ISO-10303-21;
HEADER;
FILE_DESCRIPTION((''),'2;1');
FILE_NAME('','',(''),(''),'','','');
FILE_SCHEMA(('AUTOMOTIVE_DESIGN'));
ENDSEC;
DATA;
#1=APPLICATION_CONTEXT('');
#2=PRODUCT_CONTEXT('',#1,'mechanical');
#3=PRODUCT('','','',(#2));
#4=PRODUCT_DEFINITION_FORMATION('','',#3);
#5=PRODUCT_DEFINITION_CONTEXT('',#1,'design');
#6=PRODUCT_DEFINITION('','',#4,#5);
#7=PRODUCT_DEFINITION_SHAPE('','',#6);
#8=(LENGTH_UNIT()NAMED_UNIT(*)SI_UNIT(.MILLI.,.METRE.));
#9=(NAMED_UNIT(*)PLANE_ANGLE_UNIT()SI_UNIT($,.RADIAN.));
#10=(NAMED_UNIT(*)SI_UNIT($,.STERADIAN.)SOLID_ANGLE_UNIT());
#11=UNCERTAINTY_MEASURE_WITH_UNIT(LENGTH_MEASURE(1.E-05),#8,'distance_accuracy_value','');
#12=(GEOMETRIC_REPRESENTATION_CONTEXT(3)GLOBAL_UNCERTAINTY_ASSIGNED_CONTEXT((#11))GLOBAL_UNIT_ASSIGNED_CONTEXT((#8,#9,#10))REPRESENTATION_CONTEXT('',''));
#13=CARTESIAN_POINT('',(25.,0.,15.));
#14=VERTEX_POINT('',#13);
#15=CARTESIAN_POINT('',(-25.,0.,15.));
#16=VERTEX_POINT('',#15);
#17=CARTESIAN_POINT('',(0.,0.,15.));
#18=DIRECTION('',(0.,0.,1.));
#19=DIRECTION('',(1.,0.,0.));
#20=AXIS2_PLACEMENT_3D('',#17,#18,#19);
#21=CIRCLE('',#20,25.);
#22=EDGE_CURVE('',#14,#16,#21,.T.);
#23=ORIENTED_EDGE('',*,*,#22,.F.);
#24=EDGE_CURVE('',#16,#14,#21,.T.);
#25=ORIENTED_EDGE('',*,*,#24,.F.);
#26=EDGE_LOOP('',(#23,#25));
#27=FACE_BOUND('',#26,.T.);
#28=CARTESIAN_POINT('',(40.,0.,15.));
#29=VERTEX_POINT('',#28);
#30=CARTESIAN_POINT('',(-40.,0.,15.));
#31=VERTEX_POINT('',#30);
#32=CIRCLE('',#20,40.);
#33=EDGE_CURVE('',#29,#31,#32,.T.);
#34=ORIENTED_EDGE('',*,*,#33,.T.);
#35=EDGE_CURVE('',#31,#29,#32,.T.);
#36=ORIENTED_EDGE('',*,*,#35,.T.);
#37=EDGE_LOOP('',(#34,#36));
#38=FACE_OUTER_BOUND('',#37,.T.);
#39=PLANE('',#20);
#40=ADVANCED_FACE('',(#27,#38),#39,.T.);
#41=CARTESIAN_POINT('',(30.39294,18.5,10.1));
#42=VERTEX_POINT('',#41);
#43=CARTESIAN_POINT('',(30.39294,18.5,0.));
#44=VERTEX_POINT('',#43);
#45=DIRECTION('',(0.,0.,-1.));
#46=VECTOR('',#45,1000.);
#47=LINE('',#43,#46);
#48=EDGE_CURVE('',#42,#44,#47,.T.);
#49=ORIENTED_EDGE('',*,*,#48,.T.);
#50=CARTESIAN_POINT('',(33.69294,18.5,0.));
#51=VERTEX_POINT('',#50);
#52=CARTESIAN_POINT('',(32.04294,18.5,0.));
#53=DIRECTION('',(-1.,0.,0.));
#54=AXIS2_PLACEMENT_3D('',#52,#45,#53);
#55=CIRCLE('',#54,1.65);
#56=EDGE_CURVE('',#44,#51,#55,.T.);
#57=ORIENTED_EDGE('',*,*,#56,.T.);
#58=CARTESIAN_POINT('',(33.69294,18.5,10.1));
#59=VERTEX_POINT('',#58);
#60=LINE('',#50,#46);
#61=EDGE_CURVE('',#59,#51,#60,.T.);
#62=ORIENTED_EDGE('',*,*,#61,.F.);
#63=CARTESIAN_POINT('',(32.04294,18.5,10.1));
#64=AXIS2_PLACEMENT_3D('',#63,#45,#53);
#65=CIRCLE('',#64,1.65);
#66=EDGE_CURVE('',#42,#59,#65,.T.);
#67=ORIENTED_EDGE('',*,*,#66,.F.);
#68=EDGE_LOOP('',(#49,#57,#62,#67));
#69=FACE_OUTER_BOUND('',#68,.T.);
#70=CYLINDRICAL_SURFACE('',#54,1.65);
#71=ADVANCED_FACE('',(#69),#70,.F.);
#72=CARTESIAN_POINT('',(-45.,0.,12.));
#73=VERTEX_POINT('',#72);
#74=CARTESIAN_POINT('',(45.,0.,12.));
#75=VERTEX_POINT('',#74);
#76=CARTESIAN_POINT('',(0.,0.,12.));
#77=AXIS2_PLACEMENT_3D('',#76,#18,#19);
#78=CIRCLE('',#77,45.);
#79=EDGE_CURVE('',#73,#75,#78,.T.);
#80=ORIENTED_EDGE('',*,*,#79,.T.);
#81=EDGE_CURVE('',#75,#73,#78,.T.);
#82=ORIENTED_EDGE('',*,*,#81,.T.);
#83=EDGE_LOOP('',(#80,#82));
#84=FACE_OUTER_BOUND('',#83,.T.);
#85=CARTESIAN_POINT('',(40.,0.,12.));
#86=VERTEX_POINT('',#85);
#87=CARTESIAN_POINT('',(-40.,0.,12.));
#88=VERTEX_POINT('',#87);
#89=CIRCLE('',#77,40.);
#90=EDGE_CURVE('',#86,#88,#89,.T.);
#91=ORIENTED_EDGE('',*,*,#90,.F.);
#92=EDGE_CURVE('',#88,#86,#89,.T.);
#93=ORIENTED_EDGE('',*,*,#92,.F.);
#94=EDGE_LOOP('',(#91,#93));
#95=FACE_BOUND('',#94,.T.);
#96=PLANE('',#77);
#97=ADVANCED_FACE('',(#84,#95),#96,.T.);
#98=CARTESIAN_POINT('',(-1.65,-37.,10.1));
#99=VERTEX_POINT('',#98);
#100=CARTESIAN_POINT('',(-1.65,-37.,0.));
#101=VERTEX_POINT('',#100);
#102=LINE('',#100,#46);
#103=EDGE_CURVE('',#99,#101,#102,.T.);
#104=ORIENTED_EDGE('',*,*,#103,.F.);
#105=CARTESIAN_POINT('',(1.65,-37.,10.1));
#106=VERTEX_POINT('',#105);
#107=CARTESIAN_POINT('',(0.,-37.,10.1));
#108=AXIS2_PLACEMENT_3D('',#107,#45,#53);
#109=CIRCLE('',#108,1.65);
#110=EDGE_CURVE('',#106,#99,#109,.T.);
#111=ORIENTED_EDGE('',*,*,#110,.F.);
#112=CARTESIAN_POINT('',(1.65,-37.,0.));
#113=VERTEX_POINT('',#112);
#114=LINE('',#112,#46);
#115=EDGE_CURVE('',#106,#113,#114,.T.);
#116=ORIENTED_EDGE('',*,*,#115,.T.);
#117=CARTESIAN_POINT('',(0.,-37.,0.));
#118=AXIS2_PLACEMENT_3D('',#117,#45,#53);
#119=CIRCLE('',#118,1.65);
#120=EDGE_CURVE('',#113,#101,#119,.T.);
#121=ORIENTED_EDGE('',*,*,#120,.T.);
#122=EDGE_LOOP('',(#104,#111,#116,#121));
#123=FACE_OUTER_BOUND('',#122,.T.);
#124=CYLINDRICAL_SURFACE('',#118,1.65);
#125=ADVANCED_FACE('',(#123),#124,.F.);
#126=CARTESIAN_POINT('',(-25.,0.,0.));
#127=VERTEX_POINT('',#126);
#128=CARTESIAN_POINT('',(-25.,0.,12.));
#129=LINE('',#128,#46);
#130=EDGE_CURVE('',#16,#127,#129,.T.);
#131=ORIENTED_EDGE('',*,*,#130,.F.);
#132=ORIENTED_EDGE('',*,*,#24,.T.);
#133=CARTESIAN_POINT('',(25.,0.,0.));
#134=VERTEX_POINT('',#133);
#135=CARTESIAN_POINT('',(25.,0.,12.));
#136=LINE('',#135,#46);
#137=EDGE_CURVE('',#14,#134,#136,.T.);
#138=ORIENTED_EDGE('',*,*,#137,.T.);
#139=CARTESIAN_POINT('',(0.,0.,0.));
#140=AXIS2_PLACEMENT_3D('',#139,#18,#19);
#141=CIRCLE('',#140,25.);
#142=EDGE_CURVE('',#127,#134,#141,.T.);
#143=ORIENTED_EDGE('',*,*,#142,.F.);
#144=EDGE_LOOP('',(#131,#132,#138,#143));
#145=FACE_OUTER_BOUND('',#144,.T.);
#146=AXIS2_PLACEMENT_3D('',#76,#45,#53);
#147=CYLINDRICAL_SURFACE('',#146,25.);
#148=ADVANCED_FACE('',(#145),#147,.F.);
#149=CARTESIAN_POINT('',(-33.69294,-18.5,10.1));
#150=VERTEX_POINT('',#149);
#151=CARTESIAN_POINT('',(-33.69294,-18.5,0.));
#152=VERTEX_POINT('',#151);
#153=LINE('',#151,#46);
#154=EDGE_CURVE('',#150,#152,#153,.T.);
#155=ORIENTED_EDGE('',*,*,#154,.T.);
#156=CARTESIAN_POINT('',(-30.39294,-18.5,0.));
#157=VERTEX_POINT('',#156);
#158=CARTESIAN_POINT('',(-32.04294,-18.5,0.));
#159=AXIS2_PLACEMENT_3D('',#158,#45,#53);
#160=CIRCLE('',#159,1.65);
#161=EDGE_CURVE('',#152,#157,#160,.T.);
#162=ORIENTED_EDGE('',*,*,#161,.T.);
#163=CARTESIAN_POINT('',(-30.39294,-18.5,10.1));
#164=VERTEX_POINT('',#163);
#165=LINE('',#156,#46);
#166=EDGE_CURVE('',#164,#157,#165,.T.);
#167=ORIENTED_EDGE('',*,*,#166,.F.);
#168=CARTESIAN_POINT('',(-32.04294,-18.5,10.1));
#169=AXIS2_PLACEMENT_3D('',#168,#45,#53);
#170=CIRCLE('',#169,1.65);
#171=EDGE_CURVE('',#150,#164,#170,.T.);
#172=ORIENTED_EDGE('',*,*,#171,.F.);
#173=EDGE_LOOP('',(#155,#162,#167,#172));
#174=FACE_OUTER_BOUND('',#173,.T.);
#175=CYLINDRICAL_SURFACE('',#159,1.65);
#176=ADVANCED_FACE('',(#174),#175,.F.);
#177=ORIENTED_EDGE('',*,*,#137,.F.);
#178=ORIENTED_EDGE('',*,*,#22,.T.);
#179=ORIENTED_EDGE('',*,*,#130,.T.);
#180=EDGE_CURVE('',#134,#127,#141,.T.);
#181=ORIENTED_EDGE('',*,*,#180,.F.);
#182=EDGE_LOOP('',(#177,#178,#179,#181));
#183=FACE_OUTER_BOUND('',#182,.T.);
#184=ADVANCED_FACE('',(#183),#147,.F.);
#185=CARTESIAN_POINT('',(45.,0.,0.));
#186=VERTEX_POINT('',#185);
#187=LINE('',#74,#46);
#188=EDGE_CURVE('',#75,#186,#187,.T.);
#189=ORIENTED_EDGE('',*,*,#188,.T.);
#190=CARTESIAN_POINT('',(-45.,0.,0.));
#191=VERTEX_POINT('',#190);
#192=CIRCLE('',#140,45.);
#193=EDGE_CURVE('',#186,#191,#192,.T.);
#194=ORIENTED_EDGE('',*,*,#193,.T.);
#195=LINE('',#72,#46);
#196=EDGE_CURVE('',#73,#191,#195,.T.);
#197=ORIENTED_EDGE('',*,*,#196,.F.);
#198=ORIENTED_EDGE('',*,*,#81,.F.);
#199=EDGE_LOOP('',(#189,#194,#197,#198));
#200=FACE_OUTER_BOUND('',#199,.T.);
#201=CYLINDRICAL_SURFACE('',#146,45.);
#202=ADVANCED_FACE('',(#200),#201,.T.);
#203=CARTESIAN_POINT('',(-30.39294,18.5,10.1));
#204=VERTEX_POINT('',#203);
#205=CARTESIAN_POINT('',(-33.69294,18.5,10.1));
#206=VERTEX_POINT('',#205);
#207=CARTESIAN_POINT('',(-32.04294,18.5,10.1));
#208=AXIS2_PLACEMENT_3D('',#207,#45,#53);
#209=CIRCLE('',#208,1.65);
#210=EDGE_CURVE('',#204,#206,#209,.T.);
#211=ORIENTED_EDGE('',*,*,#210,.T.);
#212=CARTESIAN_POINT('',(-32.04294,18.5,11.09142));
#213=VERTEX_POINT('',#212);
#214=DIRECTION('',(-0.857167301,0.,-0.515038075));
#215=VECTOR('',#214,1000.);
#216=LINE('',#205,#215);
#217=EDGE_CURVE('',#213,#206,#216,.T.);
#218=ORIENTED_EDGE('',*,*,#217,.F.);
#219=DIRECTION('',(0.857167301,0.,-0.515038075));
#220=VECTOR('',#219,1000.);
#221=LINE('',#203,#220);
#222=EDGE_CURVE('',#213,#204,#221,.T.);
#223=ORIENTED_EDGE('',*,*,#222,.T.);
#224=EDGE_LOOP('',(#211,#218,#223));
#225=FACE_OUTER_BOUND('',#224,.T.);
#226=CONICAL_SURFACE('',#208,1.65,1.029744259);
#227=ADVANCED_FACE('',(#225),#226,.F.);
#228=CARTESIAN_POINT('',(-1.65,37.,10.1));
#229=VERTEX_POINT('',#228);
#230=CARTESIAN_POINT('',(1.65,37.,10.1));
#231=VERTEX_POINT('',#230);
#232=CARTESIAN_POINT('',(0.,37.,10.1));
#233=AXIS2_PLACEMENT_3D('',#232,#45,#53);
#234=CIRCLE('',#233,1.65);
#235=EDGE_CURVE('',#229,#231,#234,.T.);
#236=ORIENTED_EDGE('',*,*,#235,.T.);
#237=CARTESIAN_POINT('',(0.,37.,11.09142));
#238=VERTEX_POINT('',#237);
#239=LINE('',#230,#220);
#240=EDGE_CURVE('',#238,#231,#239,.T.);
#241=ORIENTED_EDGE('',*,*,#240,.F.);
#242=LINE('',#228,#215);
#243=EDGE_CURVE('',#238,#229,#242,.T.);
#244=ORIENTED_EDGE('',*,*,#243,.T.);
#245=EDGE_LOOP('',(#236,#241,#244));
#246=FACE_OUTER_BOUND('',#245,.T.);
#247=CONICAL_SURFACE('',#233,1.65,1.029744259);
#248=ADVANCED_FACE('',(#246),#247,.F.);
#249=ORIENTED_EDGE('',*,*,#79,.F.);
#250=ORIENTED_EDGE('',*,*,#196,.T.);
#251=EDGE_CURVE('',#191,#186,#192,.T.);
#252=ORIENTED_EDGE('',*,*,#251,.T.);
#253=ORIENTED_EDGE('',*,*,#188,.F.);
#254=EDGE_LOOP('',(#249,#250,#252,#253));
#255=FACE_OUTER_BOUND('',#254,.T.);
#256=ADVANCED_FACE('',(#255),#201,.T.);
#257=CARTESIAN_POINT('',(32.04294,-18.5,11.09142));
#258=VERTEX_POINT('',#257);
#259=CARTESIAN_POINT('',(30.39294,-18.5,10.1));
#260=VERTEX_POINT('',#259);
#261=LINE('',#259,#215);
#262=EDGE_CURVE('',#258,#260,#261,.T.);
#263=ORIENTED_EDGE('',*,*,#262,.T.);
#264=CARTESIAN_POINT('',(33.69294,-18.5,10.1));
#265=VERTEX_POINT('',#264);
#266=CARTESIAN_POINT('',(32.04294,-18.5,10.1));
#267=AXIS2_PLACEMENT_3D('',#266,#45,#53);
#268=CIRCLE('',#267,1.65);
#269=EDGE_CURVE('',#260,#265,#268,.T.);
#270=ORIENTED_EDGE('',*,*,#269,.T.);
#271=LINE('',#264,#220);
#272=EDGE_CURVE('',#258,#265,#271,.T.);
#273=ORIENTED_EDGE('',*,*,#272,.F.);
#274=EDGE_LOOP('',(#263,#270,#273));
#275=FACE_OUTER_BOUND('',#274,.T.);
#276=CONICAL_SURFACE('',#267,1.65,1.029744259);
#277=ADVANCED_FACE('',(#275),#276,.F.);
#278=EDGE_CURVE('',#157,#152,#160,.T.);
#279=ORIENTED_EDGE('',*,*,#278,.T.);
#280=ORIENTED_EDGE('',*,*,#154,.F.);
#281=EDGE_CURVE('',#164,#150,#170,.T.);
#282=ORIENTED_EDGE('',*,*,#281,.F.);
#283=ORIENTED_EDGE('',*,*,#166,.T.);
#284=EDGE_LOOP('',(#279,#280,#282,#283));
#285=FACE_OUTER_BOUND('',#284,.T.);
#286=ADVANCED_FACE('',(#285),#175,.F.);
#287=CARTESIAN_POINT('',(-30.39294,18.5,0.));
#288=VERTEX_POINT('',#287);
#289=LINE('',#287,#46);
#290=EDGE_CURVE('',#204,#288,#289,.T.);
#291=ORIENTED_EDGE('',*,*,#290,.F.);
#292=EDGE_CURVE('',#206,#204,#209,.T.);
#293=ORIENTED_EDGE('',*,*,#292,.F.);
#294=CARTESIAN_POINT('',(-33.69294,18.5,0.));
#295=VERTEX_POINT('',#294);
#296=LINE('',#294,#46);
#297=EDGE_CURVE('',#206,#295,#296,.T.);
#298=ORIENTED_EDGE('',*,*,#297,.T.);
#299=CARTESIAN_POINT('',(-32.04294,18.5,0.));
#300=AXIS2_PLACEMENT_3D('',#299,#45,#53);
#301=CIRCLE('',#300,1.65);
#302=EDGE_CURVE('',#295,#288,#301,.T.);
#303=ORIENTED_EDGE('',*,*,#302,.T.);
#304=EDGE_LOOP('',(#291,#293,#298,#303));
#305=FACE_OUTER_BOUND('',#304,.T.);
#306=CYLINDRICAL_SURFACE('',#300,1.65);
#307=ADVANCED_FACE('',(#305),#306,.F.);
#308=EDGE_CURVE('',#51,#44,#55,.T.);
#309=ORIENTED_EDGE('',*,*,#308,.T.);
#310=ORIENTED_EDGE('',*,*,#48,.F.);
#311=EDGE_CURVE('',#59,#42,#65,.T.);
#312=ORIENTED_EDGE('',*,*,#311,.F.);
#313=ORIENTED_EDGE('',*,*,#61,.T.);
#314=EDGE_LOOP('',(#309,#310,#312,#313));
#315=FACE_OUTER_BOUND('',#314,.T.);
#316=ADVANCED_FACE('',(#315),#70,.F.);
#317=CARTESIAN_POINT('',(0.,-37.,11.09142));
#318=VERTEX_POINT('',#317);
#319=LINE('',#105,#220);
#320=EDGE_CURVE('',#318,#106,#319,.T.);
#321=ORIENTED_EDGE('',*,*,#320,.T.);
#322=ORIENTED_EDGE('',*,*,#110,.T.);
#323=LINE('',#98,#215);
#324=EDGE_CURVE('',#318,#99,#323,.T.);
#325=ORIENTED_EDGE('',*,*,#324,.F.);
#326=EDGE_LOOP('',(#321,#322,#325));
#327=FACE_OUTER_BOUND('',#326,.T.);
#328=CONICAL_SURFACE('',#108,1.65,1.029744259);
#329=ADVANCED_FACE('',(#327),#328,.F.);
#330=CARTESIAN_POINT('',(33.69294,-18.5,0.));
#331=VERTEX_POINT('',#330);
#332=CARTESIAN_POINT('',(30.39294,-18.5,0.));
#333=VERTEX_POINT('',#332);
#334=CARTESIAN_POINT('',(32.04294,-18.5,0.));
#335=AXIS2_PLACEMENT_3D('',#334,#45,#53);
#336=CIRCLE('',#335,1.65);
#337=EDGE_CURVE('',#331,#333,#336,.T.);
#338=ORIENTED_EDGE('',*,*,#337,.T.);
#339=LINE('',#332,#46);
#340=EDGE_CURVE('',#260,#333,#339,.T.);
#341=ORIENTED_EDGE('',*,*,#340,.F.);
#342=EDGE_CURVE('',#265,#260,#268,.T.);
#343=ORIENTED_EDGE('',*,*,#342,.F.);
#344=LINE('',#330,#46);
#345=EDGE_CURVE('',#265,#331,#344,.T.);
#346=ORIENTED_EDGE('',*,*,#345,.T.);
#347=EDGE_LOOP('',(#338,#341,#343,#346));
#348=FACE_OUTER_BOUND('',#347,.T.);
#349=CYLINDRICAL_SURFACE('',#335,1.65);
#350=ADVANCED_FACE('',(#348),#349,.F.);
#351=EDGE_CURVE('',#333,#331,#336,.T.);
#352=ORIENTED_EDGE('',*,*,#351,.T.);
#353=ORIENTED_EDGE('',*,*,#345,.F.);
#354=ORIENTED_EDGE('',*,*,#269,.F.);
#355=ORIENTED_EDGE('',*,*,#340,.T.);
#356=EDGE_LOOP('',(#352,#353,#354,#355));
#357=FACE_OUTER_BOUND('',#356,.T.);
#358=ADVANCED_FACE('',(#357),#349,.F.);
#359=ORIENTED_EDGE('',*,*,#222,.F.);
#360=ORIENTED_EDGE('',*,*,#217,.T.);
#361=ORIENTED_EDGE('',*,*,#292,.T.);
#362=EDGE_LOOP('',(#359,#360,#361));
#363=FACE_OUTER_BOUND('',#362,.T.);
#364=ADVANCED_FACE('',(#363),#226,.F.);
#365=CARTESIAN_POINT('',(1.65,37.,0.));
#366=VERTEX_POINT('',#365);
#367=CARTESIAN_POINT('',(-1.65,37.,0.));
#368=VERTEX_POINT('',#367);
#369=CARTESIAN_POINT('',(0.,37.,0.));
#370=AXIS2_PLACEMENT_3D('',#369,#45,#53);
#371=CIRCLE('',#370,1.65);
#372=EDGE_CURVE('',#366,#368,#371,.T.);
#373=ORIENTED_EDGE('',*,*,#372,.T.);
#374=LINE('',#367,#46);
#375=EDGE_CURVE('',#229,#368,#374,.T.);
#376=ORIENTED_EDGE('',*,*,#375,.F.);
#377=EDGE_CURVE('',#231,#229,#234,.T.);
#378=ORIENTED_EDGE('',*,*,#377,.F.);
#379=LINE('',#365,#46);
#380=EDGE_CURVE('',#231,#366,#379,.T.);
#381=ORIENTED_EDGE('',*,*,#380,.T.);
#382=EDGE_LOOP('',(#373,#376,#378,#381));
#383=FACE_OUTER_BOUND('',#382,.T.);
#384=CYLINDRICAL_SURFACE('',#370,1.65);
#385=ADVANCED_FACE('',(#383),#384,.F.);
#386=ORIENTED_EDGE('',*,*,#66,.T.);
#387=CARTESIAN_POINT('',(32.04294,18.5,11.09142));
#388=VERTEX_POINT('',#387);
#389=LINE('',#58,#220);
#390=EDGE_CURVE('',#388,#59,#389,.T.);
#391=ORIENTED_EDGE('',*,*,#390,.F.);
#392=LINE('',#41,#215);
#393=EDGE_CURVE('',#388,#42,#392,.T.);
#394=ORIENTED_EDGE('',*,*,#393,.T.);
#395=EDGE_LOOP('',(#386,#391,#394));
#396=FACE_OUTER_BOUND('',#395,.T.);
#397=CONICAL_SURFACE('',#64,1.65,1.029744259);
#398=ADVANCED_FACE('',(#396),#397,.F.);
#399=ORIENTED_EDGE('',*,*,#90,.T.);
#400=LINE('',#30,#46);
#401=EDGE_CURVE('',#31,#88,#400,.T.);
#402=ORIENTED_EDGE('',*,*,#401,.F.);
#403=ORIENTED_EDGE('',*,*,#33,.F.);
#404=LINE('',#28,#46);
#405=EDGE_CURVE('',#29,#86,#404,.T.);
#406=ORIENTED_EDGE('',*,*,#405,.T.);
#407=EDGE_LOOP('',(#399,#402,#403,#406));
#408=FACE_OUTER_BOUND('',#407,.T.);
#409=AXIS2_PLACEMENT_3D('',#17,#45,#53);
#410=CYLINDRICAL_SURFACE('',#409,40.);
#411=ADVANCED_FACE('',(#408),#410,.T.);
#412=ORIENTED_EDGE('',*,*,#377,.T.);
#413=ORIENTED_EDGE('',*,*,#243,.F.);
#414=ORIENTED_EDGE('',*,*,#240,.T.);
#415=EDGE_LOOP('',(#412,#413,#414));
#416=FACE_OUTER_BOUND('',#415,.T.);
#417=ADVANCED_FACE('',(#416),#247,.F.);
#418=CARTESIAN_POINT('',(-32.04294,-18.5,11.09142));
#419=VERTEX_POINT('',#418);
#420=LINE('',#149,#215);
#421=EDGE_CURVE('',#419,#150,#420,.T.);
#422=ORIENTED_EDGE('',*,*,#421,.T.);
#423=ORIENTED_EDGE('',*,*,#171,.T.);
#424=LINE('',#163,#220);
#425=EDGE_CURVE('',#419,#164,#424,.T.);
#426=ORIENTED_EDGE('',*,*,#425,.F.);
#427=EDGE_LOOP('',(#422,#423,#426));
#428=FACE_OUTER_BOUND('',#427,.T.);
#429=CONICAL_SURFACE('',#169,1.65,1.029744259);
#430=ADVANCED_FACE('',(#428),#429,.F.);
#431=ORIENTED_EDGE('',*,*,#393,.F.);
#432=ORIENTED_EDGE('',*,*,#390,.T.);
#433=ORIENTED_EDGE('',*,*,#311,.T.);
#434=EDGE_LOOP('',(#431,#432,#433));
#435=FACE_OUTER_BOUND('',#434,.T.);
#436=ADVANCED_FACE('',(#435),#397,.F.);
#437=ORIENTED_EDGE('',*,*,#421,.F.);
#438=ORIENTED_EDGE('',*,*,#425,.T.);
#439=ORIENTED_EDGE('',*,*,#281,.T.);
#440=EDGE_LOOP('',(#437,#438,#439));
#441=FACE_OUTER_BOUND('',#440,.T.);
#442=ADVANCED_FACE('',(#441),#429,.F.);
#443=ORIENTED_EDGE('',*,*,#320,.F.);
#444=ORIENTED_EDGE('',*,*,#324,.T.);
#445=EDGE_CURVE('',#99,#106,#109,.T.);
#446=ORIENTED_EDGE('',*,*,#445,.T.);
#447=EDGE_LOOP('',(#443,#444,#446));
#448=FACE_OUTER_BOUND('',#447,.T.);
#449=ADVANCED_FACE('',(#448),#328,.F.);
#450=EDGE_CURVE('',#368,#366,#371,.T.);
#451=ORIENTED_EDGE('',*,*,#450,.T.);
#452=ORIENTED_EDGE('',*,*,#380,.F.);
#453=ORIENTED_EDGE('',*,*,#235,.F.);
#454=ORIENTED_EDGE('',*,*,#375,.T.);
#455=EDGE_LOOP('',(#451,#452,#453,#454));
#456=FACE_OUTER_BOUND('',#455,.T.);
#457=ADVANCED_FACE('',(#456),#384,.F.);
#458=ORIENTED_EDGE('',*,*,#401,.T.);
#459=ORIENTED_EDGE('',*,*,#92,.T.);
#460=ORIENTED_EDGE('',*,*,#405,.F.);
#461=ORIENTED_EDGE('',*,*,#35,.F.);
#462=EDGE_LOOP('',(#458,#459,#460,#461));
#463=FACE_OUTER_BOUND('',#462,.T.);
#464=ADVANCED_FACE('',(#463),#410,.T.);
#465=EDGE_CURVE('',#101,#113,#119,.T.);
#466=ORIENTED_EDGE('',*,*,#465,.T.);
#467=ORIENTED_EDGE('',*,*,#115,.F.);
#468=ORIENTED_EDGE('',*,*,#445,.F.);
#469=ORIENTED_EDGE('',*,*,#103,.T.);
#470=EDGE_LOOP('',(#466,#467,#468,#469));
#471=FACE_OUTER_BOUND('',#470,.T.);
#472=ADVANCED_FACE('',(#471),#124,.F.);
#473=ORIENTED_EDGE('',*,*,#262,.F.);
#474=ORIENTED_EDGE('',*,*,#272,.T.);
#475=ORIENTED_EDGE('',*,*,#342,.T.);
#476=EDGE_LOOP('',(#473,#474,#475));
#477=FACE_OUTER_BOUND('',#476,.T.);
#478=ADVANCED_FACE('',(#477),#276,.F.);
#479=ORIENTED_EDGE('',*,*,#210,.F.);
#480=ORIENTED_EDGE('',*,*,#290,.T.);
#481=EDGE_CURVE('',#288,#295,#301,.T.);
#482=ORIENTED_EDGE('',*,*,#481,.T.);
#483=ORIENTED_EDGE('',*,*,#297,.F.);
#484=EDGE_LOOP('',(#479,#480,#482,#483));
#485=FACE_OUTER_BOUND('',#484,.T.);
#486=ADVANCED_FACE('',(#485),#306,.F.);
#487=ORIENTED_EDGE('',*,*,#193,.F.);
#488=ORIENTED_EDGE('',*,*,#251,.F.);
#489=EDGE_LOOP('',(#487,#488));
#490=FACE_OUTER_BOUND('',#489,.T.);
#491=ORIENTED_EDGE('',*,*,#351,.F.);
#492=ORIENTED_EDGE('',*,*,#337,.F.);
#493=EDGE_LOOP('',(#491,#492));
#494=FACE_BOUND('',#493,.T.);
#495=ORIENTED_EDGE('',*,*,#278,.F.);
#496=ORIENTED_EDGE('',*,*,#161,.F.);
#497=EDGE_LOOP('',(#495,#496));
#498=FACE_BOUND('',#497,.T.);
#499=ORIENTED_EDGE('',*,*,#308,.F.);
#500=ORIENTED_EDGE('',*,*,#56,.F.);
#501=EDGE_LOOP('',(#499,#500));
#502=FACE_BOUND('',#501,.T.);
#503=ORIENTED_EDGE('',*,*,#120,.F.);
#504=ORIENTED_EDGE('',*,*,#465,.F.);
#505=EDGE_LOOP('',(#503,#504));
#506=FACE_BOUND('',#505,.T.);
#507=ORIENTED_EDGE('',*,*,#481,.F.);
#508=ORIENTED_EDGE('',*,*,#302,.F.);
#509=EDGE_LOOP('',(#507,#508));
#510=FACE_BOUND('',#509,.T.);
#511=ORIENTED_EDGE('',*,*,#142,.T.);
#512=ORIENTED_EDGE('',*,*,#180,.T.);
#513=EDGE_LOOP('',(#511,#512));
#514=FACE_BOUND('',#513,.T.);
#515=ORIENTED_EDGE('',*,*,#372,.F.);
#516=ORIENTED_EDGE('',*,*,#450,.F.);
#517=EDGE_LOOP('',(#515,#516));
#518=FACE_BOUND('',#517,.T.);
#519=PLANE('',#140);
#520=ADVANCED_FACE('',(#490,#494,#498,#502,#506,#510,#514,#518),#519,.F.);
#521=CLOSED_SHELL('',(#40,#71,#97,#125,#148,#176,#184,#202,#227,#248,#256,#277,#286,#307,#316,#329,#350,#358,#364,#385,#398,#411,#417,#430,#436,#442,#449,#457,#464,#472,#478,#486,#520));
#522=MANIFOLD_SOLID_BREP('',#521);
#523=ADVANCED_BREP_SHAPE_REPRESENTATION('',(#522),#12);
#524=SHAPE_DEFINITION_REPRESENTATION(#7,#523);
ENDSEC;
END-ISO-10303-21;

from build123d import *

# Parameters (mm, degrees)
SKETCH1_R             = 45
SKETCH1_R_2           = 25
BOSS_EXTRUDE1_DEPTH   = 12
SKETCH2_R             = 40
SKETCH2_R_2           = 25
BOSS_EXTRUDE2_DEPTH   = 3
M4_TAPPED_HOLE2_D     = 3.3
M4_TAPPED_HOLE2_DEPTH = 10.1
M4_TAPPED_HOLE2_TIP   = 0.991420021


with BuildPart() as part:
    # Sketch1 → Boss-Extrude1 (new body)
    with BuildSketch(Plane.XY):
        Circle(SKETCH1_R)
        Circle(SKETCH1_R_2, mode=Mode.SUBTRACT)
    extrude(amount=BOSS_EXTRUDE1_DEPTH)

    # Sketch2 → Boss-Extrude2 (add)
    with BuildSketch(Plane.XY.offset(12)):
        Circle(SKETCH2_R)
        Circle(SKETCH2_R_2, mode=Mode.SUBTRACT)
    extrude(amount=BOSS_EXTRUDE2_DEPTH)

    # M4 Tapped Hole2
    with Locations(Plane(origin=(32.04293994, 18.5, 0), x_dir=(-1, 0, 0), z_dir=(0, 0, -1))):
        with Locations((0, 0), (32.04293994, 18.5), (64.08587988, 0), (64.08587988, -37), (32.04293994, -55.5), (0, -37)):
            Hole(M4_TAPPED_HOLE2_D / 2, depth=M4_TAPPED_HOLE2_DEPTH)
            with Locations((0, 0, -(M4_TAPPED_HOLE2_DEPTH + M4_TAPPED_HOLE2_TIP / 2))):  # 118° drill point
                Cone(0, M4_TAPPED_HOLE2_D / 2, M4_TAPPED_HOLE2_TIP, mode=Mode.SUBTRACT)


solid = part.part
